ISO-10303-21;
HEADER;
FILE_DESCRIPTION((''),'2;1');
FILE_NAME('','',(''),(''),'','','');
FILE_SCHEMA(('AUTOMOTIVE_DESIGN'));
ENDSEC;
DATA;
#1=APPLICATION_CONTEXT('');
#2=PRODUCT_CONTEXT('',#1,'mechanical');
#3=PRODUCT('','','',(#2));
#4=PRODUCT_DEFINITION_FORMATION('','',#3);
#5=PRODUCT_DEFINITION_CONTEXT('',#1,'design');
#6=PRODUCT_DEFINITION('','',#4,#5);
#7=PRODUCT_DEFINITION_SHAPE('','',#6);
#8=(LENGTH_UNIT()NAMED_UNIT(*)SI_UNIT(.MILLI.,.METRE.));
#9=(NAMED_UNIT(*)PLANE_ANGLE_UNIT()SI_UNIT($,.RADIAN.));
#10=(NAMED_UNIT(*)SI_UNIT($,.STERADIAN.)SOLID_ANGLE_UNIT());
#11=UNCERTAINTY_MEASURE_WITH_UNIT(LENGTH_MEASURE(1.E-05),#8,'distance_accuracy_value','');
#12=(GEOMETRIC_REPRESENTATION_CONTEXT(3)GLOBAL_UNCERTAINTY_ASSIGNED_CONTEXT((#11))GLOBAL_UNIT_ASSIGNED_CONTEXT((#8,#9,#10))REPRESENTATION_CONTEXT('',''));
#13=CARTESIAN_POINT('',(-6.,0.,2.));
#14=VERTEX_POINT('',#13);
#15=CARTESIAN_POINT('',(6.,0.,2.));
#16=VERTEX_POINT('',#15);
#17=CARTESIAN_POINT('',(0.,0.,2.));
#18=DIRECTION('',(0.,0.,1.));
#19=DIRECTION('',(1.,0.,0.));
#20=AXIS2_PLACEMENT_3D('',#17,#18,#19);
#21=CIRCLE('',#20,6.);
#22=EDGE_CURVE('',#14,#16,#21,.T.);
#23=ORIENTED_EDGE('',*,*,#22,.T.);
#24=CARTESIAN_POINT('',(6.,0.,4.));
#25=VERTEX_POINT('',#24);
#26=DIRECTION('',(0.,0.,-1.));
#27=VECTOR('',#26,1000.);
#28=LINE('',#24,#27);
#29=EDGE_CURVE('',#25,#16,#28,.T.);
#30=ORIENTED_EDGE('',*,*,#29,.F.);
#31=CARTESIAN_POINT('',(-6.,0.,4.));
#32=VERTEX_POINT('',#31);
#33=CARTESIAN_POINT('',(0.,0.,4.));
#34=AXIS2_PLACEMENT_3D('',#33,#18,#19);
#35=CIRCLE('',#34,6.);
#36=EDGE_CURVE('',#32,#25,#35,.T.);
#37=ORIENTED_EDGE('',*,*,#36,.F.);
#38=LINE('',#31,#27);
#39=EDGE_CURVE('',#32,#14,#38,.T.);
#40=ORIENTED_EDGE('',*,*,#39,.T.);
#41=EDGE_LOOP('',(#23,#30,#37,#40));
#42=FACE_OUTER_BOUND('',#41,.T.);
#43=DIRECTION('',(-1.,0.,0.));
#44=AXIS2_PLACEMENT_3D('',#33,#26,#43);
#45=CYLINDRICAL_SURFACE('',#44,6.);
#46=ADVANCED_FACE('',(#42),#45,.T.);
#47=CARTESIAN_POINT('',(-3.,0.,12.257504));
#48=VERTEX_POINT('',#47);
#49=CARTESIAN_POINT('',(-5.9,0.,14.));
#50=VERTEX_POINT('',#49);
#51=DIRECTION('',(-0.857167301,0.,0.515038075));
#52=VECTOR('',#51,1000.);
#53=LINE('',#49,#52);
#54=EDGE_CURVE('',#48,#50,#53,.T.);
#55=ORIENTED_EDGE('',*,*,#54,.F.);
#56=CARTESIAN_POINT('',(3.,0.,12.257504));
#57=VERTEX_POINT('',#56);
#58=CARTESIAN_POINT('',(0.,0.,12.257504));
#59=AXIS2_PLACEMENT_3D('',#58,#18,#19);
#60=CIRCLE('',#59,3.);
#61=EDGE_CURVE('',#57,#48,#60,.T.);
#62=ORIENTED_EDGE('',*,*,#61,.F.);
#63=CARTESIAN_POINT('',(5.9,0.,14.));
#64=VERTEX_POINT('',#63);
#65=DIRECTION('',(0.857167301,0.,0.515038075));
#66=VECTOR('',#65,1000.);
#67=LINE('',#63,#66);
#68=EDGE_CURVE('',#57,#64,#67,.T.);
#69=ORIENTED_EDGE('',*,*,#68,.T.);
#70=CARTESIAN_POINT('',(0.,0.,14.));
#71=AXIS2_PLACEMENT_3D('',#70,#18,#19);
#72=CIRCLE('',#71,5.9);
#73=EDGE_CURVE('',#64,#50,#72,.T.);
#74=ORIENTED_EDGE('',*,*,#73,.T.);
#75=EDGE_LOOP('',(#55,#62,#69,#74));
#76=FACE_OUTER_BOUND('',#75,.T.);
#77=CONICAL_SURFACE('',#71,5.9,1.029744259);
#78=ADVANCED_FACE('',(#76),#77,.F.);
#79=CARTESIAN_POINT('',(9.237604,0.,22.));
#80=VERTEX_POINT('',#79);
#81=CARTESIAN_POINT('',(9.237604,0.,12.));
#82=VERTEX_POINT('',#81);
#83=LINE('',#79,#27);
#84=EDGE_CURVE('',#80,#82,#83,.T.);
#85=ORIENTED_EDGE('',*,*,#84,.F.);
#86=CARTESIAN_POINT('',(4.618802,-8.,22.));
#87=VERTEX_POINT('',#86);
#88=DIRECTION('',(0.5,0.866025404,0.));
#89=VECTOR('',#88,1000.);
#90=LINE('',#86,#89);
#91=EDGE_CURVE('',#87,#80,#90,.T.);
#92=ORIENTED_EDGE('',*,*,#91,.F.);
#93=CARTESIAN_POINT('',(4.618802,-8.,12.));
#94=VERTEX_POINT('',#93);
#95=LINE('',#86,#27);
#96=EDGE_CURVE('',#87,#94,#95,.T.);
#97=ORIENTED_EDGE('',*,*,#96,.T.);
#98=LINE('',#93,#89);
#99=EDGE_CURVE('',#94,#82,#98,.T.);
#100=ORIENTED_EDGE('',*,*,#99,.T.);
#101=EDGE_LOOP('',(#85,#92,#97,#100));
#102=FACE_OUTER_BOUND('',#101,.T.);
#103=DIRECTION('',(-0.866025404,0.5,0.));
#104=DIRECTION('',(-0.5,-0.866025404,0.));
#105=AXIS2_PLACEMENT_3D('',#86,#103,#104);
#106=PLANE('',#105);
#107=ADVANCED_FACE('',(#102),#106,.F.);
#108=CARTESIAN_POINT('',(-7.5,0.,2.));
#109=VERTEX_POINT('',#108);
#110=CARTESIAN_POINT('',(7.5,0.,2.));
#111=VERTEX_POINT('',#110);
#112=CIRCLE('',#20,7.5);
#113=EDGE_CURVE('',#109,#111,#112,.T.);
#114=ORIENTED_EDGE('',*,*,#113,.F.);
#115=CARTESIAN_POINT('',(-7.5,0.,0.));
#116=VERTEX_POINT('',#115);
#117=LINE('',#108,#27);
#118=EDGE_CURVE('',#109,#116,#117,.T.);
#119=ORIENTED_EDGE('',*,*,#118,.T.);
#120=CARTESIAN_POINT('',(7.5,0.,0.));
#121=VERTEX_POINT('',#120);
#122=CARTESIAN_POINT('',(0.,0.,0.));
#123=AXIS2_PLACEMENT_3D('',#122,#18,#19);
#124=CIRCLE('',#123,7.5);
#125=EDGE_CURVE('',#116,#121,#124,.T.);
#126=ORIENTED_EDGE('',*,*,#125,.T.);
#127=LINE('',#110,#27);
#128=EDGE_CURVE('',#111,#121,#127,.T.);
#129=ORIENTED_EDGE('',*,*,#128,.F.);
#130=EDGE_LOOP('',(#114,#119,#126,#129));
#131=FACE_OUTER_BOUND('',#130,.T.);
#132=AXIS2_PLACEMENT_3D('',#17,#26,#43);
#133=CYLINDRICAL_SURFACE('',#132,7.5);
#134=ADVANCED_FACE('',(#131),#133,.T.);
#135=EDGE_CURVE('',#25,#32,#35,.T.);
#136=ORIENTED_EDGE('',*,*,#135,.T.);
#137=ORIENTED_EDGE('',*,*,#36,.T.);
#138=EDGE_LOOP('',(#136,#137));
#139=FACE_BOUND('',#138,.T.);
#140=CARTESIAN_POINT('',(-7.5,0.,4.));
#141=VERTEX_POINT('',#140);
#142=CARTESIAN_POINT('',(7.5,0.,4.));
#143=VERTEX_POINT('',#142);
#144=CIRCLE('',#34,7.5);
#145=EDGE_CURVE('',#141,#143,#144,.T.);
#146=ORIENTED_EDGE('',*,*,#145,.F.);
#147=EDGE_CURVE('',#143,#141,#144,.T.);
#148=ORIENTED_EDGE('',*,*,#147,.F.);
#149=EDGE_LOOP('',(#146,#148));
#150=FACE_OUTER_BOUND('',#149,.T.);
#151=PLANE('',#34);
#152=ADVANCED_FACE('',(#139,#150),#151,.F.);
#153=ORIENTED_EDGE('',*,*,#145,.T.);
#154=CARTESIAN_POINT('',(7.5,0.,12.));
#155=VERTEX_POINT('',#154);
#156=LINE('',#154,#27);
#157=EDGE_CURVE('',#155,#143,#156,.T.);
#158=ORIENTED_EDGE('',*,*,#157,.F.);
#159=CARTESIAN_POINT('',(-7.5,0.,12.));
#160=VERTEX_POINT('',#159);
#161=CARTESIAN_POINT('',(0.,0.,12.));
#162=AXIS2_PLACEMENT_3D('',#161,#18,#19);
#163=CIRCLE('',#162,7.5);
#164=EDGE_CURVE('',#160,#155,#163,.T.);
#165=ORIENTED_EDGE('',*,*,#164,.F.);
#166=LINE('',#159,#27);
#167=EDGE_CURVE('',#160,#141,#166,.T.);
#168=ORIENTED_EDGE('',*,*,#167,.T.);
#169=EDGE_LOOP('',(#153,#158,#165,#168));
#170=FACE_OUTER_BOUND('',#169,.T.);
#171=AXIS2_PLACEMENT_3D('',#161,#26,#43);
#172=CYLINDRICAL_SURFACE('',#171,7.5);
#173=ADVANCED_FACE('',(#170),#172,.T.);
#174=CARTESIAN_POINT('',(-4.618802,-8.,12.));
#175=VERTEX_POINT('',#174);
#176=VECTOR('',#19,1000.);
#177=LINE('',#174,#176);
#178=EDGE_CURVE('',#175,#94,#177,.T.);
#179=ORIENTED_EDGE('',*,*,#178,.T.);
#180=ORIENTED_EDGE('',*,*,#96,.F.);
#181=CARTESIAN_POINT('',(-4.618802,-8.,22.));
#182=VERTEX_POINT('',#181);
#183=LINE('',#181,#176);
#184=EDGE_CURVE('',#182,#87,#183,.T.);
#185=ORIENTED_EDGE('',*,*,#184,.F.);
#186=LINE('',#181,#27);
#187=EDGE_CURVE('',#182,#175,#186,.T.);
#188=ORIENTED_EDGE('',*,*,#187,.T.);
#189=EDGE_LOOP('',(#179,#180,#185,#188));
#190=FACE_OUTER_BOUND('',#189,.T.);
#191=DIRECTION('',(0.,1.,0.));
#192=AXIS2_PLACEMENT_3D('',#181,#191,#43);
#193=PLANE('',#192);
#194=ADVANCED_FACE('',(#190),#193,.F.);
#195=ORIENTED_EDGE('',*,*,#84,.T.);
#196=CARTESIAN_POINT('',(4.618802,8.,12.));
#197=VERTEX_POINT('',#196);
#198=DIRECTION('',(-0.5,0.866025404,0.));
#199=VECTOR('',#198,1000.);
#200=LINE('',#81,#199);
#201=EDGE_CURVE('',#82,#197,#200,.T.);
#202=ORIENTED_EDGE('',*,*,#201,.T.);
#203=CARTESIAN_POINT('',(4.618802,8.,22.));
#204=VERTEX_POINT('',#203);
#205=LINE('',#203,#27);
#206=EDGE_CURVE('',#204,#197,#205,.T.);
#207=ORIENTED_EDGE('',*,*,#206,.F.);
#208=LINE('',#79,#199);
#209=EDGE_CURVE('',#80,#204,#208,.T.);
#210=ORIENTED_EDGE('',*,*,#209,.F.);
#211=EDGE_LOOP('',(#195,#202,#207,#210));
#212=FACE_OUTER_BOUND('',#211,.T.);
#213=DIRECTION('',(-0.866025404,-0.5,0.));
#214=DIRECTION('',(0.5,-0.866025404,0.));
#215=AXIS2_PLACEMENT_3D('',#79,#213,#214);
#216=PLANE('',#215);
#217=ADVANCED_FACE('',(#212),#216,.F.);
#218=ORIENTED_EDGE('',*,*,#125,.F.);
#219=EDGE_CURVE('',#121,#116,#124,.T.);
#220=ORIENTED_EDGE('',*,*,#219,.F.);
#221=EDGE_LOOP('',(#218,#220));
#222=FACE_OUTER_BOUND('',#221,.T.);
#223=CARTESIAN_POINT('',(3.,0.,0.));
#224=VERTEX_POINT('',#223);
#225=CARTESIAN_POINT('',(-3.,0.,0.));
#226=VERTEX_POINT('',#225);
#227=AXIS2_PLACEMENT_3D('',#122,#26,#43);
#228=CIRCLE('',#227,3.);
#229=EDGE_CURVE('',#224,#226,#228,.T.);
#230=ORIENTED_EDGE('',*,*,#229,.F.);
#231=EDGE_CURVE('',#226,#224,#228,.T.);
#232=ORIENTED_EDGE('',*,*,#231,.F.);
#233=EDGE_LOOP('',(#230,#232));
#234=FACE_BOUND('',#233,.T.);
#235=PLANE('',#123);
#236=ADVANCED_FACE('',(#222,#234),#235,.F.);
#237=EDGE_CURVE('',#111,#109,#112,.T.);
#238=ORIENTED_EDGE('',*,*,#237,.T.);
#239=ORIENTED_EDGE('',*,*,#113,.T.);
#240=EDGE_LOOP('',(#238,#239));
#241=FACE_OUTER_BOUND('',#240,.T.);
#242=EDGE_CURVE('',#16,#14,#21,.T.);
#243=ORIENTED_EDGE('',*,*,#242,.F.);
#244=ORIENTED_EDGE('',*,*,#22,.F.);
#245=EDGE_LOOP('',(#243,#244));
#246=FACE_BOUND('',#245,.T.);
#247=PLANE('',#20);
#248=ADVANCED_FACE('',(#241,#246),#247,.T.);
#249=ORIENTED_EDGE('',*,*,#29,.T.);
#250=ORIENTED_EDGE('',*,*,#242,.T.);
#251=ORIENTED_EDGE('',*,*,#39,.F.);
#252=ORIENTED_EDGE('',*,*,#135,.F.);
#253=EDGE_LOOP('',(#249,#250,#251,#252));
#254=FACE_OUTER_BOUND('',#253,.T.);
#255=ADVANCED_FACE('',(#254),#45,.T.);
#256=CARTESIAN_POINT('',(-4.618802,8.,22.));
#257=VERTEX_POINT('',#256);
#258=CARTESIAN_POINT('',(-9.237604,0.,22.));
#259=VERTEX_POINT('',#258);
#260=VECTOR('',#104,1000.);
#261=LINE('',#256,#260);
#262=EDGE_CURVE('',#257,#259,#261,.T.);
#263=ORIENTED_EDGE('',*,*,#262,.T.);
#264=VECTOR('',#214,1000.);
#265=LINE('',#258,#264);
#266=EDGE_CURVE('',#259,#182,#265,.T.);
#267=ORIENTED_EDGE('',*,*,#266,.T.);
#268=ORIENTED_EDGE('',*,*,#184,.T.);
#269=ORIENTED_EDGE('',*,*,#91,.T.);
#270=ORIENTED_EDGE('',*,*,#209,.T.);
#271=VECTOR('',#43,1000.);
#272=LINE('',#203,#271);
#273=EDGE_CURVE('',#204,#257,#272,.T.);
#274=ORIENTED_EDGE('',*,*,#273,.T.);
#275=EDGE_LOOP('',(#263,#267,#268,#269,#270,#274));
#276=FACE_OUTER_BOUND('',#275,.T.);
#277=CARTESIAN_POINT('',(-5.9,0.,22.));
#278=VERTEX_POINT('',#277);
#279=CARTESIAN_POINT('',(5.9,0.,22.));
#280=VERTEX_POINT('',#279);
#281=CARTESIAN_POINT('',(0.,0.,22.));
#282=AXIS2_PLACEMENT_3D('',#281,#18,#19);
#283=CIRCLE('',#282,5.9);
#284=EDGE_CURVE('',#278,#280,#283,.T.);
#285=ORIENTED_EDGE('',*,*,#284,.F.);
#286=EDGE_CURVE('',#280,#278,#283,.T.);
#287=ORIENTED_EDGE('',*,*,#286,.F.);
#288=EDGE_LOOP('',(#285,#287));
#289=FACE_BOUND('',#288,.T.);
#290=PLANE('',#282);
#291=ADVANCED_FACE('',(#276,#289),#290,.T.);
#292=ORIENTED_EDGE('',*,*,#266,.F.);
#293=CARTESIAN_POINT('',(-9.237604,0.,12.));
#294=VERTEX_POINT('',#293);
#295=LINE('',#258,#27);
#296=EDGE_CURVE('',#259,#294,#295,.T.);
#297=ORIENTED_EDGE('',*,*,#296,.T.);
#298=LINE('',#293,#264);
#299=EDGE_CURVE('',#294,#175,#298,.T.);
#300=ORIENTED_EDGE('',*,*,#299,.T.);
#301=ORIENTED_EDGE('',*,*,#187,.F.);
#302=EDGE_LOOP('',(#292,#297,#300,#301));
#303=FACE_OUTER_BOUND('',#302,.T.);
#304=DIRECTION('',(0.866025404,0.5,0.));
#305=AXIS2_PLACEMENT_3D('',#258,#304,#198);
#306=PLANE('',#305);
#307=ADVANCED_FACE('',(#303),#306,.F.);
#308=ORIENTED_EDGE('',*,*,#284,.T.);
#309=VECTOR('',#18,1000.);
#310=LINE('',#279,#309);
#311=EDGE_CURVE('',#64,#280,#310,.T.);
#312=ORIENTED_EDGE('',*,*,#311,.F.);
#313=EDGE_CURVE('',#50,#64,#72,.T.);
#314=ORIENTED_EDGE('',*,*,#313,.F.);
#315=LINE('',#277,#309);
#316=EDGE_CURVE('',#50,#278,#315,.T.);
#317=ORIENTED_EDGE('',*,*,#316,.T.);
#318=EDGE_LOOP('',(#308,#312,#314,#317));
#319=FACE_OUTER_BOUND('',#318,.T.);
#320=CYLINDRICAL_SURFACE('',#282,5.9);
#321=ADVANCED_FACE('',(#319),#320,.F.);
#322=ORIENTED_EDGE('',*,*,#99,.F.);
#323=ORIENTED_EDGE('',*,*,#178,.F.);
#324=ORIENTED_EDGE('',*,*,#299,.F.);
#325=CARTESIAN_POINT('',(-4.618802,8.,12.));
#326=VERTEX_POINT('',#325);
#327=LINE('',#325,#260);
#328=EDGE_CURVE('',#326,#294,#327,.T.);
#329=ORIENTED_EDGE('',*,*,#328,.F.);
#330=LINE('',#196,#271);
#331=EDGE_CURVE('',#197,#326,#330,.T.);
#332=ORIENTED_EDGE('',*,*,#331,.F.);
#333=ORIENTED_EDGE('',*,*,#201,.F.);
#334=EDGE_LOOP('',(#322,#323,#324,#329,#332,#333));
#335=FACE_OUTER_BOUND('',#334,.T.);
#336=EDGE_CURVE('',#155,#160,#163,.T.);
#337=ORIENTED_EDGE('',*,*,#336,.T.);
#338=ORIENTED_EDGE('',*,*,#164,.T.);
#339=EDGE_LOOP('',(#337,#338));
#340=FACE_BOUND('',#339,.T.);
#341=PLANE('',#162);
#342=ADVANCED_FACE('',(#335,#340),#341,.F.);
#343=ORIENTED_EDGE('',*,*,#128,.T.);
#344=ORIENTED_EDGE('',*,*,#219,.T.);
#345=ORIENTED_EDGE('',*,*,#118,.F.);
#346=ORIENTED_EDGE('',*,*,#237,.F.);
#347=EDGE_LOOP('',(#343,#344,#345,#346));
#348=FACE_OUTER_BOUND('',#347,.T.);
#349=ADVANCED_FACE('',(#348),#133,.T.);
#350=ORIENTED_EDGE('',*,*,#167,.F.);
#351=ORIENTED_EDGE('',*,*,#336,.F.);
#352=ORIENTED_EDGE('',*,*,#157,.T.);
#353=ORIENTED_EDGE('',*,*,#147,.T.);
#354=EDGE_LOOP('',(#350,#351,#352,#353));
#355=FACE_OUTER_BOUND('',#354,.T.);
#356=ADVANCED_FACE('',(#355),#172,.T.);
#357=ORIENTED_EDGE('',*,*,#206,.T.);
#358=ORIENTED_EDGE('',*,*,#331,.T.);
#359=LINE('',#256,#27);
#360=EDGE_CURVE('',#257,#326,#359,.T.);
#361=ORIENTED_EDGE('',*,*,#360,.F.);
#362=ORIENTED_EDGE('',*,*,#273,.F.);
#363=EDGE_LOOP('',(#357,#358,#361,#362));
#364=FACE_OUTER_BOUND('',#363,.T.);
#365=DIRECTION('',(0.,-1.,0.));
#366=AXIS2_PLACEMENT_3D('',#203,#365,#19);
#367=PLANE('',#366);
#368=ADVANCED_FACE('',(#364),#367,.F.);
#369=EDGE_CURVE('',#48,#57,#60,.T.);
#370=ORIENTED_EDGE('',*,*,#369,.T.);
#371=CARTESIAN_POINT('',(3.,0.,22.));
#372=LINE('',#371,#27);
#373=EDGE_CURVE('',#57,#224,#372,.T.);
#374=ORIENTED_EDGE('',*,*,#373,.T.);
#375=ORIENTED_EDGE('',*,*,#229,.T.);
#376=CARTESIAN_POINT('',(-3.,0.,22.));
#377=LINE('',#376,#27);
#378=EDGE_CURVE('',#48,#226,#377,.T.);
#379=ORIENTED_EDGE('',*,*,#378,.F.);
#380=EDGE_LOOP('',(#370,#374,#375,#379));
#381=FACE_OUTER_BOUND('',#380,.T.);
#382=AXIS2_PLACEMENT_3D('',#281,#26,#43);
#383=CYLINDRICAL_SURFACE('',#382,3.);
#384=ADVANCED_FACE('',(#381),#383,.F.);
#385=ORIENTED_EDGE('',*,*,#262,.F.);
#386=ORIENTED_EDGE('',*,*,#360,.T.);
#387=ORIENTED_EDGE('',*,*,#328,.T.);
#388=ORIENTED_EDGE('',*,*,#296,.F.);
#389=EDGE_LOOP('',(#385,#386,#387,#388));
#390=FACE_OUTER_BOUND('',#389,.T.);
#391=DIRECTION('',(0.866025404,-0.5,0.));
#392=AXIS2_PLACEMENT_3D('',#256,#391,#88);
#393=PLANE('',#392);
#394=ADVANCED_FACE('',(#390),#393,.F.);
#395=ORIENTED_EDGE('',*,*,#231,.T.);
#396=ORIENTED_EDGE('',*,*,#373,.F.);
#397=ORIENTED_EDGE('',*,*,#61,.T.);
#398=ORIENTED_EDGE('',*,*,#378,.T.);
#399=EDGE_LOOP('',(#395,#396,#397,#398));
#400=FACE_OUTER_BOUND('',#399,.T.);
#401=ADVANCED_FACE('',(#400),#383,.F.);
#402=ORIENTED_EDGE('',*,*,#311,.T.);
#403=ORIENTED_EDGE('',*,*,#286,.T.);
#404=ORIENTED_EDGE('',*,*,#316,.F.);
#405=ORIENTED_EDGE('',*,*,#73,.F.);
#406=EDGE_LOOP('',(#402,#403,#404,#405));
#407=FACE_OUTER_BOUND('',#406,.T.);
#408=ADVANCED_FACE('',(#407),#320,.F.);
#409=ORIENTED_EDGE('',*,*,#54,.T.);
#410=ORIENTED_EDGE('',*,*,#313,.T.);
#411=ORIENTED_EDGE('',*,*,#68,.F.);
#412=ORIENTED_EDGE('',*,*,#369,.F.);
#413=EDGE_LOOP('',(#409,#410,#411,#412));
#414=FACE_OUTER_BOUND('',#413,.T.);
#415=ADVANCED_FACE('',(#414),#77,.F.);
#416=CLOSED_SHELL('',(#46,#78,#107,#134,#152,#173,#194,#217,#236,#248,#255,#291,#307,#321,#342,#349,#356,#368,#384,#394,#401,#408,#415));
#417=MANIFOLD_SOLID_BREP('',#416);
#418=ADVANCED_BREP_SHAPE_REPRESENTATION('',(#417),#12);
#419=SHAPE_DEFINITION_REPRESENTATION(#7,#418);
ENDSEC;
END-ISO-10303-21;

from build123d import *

# Parameters (mm, degrees)
SKETCH1_R               = 7.5
BOSS_EXTRUDE1_DEPTH     = 2
SKETCH2_R               = 6
BOSS_EXTRUDE2_DEPTH     = 2
SKETCH3_R               = 7.5
BOSS_EXTRUDE3_DEPTH     = 8
BOSS_EXTRUDE4_DEPTH     = 10
SKETCH5_R               = 3
CUT_EXTRUDE1_DEPTH      = 26.166114784
G1_4_TAPPED_HOLE1_D     = 11.8
G1_4_TAPPED_HOLE1_DEPTH = 8
G1_4_TAPPED_HOLE1_TIP   = 3.545077652


with BuildPart() as part:
    # Sketch1 → Boss-Extrude1 (new body)
    with BuildSketch(Plane.XY):
        Circle(SKETCH1_R)
    extrude(amount=BOSS_EXTRUDE1_DEPTH)

    # Sketch2 → Boss-Extrude2 (add)
    with BuildSketch(Plane.XY.offset(2)):
        Circle(SKETCH2_R)
    extrude(amount=BOSS_EXTRUDE2_DEPTH)

    # Sketch3 → Boss-Extrude3 (add)
    with BuildSketch(Plane.XY.offset(4)):
        Circle(SKETCH3_R)
    extrude(amount=BOSS_EXTRUDE3_DEPTH)

    # Sketch4 → Boss-Extrude4 (add)
    with BuildSketch(Plane.XY.offset(12)):
        Polygon((9.237604307, 0), (4.618802154, 8), (-4.618802154, 8), (-9.237604307, 0), (-4.618802154, -8), (4.618802154, -8), align=None)
    extrude(amount=BOSS_EXTRUDE4_DEPTH)

    # Sketch5 → Cut-Extrude1 (cut, through all)
    with BuildSketch(Plane(origin=(0, 0, 0), x_dir=(-1, 0, 0), z_dir=(0, 0, -1))):
        Circle(SKETCH5_R)
    extrude(amount=-CUT_EXTRUDE1_DEPTH, mode=Mode.SUBTRACT)

    # G1/4 Tapped Hole1
    with Locations(Plane.XY.offset(22)):
        with Locations((0, 0)):
            Hole(G1_4_TAPPED_HOLE1_D / 2, depth=G1_4_TAPPED_HOLE1_DEPTH)
            with Locations((0, 0, -(G1_4_TAPPED_HOLE1_DEPTH + G1_4_TAPPED_HOLE1_TIP / 2))):  # 118° drill point
                Cone(0, G1_4_TAPPED_HOLE1_D / 2, G1_4_TAPPED_HOLE1_TIP, mode=Mode.SUBTRACT)


solid = part.part
